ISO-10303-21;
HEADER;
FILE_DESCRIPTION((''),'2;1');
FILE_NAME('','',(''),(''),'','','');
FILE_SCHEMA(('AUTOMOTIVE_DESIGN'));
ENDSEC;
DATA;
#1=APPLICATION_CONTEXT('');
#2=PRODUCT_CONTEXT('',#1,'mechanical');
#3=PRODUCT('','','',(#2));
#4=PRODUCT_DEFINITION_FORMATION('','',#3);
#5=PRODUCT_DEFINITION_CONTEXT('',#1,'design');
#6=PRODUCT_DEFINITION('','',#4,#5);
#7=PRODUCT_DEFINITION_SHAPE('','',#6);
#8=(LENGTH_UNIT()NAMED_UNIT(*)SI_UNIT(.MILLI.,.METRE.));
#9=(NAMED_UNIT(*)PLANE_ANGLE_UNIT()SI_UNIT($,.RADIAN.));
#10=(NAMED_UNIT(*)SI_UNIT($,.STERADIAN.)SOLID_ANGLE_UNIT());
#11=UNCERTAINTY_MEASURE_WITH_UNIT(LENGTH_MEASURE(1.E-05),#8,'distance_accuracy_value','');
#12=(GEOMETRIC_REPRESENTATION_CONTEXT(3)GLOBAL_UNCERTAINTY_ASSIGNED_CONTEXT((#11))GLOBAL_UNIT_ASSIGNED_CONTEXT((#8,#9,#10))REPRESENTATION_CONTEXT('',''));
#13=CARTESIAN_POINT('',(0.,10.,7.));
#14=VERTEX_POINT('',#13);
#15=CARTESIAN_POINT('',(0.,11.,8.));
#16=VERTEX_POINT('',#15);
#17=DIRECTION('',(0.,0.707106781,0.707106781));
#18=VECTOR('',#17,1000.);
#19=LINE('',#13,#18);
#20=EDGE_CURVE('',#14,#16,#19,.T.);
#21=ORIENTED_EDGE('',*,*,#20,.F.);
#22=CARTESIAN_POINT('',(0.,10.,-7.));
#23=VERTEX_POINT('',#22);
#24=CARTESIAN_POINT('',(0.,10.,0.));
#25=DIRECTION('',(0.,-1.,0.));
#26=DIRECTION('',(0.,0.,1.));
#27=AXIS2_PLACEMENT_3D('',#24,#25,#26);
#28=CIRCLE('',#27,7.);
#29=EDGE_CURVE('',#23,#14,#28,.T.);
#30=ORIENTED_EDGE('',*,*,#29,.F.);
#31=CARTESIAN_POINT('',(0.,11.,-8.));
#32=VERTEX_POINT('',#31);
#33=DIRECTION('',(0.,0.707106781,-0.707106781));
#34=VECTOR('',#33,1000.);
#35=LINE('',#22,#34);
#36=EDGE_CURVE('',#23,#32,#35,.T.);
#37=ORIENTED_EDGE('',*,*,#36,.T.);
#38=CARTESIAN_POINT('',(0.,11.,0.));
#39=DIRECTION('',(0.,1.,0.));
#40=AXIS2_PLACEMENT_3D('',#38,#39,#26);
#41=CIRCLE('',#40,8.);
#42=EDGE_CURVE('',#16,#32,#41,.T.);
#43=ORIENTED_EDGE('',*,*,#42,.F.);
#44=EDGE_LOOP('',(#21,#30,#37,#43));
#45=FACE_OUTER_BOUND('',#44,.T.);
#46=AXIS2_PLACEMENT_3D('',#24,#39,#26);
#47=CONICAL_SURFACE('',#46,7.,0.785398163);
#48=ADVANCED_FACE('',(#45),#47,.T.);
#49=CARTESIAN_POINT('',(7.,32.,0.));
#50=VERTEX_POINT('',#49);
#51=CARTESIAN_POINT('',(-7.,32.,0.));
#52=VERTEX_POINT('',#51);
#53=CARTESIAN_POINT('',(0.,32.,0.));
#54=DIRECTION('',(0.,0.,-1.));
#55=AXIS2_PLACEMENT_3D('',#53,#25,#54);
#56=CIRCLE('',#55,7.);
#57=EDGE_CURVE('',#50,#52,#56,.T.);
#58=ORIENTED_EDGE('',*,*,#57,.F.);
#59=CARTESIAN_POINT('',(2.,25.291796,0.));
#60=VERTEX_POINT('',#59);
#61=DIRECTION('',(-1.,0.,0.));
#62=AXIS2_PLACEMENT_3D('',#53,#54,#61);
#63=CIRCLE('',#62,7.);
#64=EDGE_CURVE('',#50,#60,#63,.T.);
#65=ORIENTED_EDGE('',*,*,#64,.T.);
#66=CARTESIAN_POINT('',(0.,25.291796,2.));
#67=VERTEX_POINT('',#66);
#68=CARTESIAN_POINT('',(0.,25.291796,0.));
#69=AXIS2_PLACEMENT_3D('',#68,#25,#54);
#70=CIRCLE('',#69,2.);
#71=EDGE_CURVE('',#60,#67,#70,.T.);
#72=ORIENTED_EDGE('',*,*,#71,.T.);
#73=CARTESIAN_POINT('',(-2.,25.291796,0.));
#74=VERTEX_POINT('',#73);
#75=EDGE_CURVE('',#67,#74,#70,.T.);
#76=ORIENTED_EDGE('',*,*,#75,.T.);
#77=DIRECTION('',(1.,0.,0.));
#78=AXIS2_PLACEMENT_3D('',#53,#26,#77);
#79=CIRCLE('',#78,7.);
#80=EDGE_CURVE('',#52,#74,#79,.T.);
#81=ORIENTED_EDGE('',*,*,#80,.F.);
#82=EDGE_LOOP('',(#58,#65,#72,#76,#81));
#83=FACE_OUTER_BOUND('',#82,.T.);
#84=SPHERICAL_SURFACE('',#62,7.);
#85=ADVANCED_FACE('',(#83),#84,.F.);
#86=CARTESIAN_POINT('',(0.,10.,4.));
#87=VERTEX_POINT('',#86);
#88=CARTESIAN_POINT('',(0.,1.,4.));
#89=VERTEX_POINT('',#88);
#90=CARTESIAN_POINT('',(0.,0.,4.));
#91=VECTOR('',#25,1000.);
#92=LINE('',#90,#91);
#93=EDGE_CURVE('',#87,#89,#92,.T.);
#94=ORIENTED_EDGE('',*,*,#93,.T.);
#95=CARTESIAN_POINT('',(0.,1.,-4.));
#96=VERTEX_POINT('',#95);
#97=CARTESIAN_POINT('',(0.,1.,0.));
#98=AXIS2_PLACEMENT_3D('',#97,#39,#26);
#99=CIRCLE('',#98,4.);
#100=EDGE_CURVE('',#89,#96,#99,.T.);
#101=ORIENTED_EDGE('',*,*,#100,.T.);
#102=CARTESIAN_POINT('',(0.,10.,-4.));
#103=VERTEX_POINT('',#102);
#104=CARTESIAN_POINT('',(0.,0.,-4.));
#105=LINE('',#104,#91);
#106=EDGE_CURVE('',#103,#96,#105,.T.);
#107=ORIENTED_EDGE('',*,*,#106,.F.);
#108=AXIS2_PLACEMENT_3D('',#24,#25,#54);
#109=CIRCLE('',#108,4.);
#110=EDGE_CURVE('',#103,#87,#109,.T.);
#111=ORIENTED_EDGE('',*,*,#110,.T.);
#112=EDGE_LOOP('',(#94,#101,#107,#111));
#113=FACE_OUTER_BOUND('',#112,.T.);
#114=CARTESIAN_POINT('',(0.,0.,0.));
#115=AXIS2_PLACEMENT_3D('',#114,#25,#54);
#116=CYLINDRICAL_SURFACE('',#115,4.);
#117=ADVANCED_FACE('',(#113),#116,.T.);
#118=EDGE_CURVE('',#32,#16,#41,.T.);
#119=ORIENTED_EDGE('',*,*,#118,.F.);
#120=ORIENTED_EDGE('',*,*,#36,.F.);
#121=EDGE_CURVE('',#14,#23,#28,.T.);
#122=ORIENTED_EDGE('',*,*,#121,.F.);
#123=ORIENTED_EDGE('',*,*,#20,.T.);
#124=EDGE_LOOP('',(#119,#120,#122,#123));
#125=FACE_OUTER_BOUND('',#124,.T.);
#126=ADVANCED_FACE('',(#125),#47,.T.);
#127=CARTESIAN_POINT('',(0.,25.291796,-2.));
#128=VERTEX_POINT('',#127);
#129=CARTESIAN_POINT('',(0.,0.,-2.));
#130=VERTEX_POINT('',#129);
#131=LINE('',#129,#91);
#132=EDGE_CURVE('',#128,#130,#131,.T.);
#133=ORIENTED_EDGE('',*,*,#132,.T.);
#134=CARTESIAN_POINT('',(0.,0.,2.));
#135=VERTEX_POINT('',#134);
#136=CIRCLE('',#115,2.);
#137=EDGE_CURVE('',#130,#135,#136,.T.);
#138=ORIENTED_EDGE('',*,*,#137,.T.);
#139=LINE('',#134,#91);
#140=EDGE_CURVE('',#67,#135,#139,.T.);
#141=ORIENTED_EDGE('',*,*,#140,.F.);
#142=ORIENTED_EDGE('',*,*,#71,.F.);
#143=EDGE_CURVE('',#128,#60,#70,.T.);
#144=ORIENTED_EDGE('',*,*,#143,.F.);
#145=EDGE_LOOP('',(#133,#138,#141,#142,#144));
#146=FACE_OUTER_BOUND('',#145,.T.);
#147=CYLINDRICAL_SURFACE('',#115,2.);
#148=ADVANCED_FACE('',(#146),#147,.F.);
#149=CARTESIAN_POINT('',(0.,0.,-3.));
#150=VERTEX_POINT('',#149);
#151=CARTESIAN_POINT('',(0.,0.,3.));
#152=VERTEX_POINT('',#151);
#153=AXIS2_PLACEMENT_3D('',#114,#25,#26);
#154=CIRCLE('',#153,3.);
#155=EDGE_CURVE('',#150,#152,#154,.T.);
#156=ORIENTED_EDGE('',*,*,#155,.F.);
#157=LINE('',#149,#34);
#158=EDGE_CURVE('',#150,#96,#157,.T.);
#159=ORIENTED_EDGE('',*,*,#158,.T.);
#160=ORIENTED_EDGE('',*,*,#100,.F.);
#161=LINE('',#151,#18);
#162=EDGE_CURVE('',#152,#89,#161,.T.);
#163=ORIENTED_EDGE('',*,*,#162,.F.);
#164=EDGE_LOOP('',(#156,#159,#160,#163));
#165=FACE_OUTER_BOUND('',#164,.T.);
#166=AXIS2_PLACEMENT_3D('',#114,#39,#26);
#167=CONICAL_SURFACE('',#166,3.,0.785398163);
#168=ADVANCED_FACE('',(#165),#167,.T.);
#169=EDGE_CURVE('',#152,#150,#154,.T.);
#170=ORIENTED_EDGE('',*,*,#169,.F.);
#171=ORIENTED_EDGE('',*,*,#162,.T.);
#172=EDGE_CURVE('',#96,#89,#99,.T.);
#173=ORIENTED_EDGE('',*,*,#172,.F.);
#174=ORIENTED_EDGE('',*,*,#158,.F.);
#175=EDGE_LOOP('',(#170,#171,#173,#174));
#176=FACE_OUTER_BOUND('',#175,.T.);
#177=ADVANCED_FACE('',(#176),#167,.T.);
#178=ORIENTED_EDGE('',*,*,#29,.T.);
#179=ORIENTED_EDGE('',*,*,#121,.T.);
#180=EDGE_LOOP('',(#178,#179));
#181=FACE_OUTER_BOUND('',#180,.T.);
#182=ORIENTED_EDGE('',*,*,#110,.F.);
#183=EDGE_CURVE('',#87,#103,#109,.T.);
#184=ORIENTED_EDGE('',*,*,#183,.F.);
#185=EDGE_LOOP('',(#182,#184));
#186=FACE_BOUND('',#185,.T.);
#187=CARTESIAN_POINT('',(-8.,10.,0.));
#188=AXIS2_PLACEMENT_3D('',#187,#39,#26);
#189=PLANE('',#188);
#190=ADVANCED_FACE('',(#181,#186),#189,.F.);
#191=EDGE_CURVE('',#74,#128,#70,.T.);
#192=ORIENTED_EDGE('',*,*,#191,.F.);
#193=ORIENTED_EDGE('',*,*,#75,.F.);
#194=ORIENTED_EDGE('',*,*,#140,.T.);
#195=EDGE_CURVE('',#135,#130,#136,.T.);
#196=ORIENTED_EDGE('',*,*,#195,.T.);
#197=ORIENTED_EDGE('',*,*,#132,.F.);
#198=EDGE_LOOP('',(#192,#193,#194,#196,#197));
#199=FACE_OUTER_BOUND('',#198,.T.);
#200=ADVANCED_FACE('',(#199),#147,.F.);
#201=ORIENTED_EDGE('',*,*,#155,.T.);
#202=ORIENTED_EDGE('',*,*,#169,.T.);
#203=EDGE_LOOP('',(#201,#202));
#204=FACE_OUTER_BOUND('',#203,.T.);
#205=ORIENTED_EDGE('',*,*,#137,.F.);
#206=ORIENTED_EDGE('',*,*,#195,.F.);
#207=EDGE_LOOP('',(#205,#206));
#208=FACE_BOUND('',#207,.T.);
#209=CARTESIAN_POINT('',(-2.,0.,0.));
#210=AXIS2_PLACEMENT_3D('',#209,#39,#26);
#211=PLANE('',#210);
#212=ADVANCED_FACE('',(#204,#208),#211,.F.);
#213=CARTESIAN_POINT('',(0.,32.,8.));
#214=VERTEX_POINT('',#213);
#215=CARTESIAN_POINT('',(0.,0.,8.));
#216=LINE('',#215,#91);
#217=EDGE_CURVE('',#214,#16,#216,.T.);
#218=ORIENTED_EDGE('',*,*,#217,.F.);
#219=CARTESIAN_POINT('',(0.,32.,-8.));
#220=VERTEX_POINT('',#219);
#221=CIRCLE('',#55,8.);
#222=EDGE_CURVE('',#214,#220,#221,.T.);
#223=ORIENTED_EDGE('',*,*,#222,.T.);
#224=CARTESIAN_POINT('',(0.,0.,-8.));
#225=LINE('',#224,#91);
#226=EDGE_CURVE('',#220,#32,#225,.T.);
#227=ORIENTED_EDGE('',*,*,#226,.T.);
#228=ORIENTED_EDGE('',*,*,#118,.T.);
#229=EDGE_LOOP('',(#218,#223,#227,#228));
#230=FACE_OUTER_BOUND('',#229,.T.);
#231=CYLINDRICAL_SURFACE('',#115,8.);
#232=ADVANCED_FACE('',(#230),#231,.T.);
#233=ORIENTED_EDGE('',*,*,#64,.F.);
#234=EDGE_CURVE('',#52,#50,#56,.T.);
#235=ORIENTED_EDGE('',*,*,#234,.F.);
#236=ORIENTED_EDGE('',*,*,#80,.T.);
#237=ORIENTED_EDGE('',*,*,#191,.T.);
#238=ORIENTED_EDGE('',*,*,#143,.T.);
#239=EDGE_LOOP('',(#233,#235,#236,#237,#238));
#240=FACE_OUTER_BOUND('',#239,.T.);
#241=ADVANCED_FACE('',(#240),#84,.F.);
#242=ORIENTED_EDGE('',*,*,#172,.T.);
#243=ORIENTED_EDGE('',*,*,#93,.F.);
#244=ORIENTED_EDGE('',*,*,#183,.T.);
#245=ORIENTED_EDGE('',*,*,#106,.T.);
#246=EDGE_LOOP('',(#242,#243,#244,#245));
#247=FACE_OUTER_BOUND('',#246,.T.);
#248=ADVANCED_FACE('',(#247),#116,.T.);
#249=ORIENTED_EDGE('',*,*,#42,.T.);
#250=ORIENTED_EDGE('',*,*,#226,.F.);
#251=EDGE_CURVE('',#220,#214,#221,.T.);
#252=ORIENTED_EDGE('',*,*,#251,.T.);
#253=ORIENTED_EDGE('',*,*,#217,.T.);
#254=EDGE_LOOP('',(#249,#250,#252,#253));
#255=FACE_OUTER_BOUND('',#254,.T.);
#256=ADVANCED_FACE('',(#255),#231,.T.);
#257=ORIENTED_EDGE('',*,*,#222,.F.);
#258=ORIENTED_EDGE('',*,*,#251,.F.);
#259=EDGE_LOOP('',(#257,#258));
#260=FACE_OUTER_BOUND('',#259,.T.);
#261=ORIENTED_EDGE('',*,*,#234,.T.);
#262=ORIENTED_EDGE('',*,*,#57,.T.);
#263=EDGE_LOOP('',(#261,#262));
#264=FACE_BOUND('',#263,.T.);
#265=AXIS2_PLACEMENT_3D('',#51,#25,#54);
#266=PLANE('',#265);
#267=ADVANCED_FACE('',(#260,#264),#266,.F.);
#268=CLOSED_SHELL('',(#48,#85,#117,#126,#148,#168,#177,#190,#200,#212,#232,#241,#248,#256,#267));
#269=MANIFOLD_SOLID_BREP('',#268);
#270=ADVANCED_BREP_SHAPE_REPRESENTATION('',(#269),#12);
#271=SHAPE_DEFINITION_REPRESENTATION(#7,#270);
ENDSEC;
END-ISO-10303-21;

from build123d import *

# Parameters (mm, degrees)
CHAMFER1_SIZE = 1


with BuildPart() as part:
    # Sketch1 → Revolve2 (revolve)
    with BuildSketch(Plane.XY, mode=Mode.PRIVATE) as revolve2_sk:
        with BuildLine():
            Line((-2, 0), (-2, 25.291796068))
            ThreePointArc((-2, 25.291796068), (-5.61248608, 27.816699867), (-7, 32))
            Line((-7, 32), (-8, 32))
            Line((-8, 32), (-8, 10))
            Line((-8, 10), (-4, 10))
            Line((-4, 10), (-4, 0))
            Line((-4, 0), (-2, 0))
        make_face()
    revolve(revolve2_sk.sketch.rotate(Axis((0, 0, 0), (0, 1, 0)), 270), axis=Axis((0, 0, 0), (0, 1, 0)))

    # Chamfer1
    chamfer1_edges = [part.edges().sort_by_distance(p)[0] for p in [
        (0, 10, 8),
        (0, 0, 4),
    ]]
    chamfer(chamfer1_edges, length=CHAMFER1_SIZE)


solid = part.part
